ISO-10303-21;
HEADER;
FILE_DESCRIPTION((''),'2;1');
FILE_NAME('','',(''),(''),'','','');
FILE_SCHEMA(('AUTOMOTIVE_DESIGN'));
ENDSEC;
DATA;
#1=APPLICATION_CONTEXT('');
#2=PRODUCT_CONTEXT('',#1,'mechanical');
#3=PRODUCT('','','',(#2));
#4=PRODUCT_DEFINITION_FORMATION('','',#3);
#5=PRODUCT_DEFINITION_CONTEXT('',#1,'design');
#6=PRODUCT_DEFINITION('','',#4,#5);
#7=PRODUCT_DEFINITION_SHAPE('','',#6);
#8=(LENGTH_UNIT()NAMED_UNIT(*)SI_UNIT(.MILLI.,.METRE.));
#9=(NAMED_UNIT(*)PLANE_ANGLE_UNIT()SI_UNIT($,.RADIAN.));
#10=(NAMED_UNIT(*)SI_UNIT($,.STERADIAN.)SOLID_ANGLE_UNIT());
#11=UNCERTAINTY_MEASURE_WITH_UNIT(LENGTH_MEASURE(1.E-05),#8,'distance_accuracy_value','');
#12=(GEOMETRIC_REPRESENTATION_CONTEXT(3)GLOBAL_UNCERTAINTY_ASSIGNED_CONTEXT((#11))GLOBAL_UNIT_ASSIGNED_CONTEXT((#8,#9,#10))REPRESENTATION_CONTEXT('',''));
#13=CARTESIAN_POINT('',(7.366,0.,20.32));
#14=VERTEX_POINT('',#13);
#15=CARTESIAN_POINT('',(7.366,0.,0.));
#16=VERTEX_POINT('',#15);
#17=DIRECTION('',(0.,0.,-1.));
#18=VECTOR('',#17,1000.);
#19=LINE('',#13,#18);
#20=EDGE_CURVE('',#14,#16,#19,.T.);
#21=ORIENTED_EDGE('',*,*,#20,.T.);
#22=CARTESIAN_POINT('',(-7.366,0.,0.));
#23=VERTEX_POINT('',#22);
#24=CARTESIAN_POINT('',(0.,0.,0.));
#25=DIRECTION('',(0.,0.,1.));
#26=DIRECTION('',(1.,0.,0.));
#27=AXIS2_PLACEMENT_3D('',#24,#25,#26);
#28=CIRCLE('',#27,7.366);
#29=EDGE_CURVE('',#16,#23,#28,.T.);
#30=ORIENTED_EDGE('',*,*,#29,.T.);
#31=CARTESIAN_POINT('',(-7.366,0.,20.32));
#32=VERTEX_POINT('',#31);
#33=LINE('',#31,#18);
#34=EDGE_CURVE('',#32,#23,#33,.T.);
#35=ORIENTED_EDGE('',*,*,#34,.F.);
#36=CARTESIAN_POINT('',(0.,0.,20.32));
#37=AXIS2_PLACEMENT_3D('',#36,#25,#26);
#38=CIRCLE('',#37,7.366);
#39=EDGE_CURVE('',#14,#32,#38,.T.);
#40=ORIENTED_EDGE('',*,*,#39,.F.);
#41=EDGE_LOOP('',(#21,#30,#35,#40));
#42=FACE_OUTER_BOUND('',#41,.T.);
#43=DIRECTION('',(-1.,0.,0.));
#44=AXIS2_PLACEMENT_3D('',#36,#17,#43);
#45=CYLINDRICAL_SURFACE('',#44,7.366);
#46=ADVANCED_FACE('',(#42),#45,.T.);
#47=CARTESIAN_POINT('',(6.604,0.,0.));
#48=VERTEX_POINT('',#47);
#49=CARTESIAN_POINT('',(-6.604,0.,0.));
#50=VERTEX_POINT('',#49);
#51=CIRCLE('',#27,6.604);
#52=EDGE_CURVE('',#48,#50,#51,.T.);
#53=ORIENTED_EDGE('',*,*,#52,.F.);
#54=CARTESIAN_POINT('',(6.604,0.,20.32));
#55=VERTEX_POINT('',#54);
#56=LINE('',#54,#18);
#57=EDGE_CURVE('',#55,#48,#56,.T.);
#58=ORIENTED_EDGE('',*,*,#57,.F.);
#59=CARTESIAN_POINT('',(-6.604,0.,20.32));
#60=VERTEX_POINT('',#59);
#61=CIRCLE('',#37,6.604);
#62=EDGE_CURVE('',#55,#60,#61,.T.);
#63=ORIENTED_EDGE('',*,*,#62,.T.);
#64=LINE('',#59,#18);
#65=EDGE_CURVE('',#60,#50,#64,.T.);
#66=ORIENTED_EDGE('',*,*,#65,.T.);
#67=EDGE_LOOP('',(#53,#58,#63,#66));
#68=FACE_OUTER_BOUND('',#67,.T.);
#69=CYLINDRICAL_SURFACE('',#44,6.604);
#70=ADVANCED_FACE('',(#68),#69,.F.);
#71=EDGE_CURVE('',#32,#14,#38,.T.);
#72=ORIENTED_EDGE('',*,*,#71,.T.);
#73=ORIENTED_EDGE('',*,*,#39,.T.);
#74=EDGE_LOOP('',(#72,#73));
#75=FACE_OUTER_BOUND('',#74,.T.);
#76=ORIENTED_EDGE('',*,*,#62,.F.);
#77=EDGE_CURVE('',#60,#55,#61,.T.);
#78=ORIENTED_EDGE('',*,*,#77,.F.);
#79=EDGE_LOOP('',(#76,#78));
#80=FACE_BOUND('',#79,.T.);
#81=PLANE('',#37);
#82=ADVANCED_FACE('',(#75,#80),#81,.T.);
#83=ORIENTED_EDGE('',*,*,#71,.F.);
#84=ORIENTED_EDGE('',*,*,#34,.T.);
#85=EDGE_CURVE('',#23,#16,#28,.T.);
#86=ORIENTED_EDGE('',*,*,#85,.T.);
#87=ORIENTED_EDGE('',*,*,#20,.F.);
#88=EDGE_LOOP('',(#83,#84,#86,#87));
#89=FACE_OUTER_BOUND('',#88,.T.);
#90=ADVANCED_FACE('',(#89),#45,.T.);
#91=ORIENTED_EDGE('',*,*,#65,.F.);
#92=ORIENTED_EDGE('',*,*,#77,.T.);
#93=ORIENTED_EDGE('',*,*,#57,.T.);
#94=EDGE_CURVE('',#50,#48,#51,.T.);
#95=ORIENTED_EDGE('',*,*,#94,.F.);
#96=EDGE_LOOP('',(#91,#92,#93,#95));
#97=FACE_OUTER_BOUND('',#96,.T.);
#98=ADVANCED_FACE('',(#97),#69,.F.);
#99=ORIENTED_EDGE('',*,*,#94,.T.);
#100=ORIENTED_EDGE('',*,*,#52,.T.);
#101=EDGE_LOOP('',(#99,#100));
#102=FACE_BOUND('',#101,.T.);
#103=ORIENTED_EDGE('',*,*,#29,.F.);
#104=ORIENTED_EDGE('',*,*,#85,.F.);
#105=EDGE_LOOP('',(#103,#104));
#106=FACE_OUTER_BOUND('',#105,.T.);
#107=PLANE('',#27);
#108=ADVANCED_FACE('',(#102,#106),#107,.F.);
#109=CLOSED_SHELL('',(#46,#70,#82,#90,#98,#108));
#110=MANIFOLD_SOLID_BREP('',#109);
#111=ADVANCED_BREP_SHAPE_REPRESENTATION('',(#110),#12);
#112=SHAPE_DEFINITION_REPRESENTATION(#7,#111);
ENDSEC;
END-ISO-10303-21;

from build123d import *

# Parameters (mm, degrees)
SKETCH1_R           = 3.683
SKETCH1_R_2         = 3.302
BOSS_EXTRUDE1_DEPTH = 10.16
SCALE1_SCALE        = 2


with BuildPart() as part:
    # Sketch1 → Boss-Extrude1 (new body)
    with BuildSketch(Plane.XY):
        Circle(SKETCH1_R)
        Circle(SKETCH1_R_2, mode=Mode.SUBTRACT)
    extrude(amount=BOSS_EXTRUDE1_DEPTH)


with BuildPart() as part_1:
    # Scale1: scaled about (0, 0, 0)
    add(part.part.scale(SCALE1_SCALE))


solid = part_1.part
